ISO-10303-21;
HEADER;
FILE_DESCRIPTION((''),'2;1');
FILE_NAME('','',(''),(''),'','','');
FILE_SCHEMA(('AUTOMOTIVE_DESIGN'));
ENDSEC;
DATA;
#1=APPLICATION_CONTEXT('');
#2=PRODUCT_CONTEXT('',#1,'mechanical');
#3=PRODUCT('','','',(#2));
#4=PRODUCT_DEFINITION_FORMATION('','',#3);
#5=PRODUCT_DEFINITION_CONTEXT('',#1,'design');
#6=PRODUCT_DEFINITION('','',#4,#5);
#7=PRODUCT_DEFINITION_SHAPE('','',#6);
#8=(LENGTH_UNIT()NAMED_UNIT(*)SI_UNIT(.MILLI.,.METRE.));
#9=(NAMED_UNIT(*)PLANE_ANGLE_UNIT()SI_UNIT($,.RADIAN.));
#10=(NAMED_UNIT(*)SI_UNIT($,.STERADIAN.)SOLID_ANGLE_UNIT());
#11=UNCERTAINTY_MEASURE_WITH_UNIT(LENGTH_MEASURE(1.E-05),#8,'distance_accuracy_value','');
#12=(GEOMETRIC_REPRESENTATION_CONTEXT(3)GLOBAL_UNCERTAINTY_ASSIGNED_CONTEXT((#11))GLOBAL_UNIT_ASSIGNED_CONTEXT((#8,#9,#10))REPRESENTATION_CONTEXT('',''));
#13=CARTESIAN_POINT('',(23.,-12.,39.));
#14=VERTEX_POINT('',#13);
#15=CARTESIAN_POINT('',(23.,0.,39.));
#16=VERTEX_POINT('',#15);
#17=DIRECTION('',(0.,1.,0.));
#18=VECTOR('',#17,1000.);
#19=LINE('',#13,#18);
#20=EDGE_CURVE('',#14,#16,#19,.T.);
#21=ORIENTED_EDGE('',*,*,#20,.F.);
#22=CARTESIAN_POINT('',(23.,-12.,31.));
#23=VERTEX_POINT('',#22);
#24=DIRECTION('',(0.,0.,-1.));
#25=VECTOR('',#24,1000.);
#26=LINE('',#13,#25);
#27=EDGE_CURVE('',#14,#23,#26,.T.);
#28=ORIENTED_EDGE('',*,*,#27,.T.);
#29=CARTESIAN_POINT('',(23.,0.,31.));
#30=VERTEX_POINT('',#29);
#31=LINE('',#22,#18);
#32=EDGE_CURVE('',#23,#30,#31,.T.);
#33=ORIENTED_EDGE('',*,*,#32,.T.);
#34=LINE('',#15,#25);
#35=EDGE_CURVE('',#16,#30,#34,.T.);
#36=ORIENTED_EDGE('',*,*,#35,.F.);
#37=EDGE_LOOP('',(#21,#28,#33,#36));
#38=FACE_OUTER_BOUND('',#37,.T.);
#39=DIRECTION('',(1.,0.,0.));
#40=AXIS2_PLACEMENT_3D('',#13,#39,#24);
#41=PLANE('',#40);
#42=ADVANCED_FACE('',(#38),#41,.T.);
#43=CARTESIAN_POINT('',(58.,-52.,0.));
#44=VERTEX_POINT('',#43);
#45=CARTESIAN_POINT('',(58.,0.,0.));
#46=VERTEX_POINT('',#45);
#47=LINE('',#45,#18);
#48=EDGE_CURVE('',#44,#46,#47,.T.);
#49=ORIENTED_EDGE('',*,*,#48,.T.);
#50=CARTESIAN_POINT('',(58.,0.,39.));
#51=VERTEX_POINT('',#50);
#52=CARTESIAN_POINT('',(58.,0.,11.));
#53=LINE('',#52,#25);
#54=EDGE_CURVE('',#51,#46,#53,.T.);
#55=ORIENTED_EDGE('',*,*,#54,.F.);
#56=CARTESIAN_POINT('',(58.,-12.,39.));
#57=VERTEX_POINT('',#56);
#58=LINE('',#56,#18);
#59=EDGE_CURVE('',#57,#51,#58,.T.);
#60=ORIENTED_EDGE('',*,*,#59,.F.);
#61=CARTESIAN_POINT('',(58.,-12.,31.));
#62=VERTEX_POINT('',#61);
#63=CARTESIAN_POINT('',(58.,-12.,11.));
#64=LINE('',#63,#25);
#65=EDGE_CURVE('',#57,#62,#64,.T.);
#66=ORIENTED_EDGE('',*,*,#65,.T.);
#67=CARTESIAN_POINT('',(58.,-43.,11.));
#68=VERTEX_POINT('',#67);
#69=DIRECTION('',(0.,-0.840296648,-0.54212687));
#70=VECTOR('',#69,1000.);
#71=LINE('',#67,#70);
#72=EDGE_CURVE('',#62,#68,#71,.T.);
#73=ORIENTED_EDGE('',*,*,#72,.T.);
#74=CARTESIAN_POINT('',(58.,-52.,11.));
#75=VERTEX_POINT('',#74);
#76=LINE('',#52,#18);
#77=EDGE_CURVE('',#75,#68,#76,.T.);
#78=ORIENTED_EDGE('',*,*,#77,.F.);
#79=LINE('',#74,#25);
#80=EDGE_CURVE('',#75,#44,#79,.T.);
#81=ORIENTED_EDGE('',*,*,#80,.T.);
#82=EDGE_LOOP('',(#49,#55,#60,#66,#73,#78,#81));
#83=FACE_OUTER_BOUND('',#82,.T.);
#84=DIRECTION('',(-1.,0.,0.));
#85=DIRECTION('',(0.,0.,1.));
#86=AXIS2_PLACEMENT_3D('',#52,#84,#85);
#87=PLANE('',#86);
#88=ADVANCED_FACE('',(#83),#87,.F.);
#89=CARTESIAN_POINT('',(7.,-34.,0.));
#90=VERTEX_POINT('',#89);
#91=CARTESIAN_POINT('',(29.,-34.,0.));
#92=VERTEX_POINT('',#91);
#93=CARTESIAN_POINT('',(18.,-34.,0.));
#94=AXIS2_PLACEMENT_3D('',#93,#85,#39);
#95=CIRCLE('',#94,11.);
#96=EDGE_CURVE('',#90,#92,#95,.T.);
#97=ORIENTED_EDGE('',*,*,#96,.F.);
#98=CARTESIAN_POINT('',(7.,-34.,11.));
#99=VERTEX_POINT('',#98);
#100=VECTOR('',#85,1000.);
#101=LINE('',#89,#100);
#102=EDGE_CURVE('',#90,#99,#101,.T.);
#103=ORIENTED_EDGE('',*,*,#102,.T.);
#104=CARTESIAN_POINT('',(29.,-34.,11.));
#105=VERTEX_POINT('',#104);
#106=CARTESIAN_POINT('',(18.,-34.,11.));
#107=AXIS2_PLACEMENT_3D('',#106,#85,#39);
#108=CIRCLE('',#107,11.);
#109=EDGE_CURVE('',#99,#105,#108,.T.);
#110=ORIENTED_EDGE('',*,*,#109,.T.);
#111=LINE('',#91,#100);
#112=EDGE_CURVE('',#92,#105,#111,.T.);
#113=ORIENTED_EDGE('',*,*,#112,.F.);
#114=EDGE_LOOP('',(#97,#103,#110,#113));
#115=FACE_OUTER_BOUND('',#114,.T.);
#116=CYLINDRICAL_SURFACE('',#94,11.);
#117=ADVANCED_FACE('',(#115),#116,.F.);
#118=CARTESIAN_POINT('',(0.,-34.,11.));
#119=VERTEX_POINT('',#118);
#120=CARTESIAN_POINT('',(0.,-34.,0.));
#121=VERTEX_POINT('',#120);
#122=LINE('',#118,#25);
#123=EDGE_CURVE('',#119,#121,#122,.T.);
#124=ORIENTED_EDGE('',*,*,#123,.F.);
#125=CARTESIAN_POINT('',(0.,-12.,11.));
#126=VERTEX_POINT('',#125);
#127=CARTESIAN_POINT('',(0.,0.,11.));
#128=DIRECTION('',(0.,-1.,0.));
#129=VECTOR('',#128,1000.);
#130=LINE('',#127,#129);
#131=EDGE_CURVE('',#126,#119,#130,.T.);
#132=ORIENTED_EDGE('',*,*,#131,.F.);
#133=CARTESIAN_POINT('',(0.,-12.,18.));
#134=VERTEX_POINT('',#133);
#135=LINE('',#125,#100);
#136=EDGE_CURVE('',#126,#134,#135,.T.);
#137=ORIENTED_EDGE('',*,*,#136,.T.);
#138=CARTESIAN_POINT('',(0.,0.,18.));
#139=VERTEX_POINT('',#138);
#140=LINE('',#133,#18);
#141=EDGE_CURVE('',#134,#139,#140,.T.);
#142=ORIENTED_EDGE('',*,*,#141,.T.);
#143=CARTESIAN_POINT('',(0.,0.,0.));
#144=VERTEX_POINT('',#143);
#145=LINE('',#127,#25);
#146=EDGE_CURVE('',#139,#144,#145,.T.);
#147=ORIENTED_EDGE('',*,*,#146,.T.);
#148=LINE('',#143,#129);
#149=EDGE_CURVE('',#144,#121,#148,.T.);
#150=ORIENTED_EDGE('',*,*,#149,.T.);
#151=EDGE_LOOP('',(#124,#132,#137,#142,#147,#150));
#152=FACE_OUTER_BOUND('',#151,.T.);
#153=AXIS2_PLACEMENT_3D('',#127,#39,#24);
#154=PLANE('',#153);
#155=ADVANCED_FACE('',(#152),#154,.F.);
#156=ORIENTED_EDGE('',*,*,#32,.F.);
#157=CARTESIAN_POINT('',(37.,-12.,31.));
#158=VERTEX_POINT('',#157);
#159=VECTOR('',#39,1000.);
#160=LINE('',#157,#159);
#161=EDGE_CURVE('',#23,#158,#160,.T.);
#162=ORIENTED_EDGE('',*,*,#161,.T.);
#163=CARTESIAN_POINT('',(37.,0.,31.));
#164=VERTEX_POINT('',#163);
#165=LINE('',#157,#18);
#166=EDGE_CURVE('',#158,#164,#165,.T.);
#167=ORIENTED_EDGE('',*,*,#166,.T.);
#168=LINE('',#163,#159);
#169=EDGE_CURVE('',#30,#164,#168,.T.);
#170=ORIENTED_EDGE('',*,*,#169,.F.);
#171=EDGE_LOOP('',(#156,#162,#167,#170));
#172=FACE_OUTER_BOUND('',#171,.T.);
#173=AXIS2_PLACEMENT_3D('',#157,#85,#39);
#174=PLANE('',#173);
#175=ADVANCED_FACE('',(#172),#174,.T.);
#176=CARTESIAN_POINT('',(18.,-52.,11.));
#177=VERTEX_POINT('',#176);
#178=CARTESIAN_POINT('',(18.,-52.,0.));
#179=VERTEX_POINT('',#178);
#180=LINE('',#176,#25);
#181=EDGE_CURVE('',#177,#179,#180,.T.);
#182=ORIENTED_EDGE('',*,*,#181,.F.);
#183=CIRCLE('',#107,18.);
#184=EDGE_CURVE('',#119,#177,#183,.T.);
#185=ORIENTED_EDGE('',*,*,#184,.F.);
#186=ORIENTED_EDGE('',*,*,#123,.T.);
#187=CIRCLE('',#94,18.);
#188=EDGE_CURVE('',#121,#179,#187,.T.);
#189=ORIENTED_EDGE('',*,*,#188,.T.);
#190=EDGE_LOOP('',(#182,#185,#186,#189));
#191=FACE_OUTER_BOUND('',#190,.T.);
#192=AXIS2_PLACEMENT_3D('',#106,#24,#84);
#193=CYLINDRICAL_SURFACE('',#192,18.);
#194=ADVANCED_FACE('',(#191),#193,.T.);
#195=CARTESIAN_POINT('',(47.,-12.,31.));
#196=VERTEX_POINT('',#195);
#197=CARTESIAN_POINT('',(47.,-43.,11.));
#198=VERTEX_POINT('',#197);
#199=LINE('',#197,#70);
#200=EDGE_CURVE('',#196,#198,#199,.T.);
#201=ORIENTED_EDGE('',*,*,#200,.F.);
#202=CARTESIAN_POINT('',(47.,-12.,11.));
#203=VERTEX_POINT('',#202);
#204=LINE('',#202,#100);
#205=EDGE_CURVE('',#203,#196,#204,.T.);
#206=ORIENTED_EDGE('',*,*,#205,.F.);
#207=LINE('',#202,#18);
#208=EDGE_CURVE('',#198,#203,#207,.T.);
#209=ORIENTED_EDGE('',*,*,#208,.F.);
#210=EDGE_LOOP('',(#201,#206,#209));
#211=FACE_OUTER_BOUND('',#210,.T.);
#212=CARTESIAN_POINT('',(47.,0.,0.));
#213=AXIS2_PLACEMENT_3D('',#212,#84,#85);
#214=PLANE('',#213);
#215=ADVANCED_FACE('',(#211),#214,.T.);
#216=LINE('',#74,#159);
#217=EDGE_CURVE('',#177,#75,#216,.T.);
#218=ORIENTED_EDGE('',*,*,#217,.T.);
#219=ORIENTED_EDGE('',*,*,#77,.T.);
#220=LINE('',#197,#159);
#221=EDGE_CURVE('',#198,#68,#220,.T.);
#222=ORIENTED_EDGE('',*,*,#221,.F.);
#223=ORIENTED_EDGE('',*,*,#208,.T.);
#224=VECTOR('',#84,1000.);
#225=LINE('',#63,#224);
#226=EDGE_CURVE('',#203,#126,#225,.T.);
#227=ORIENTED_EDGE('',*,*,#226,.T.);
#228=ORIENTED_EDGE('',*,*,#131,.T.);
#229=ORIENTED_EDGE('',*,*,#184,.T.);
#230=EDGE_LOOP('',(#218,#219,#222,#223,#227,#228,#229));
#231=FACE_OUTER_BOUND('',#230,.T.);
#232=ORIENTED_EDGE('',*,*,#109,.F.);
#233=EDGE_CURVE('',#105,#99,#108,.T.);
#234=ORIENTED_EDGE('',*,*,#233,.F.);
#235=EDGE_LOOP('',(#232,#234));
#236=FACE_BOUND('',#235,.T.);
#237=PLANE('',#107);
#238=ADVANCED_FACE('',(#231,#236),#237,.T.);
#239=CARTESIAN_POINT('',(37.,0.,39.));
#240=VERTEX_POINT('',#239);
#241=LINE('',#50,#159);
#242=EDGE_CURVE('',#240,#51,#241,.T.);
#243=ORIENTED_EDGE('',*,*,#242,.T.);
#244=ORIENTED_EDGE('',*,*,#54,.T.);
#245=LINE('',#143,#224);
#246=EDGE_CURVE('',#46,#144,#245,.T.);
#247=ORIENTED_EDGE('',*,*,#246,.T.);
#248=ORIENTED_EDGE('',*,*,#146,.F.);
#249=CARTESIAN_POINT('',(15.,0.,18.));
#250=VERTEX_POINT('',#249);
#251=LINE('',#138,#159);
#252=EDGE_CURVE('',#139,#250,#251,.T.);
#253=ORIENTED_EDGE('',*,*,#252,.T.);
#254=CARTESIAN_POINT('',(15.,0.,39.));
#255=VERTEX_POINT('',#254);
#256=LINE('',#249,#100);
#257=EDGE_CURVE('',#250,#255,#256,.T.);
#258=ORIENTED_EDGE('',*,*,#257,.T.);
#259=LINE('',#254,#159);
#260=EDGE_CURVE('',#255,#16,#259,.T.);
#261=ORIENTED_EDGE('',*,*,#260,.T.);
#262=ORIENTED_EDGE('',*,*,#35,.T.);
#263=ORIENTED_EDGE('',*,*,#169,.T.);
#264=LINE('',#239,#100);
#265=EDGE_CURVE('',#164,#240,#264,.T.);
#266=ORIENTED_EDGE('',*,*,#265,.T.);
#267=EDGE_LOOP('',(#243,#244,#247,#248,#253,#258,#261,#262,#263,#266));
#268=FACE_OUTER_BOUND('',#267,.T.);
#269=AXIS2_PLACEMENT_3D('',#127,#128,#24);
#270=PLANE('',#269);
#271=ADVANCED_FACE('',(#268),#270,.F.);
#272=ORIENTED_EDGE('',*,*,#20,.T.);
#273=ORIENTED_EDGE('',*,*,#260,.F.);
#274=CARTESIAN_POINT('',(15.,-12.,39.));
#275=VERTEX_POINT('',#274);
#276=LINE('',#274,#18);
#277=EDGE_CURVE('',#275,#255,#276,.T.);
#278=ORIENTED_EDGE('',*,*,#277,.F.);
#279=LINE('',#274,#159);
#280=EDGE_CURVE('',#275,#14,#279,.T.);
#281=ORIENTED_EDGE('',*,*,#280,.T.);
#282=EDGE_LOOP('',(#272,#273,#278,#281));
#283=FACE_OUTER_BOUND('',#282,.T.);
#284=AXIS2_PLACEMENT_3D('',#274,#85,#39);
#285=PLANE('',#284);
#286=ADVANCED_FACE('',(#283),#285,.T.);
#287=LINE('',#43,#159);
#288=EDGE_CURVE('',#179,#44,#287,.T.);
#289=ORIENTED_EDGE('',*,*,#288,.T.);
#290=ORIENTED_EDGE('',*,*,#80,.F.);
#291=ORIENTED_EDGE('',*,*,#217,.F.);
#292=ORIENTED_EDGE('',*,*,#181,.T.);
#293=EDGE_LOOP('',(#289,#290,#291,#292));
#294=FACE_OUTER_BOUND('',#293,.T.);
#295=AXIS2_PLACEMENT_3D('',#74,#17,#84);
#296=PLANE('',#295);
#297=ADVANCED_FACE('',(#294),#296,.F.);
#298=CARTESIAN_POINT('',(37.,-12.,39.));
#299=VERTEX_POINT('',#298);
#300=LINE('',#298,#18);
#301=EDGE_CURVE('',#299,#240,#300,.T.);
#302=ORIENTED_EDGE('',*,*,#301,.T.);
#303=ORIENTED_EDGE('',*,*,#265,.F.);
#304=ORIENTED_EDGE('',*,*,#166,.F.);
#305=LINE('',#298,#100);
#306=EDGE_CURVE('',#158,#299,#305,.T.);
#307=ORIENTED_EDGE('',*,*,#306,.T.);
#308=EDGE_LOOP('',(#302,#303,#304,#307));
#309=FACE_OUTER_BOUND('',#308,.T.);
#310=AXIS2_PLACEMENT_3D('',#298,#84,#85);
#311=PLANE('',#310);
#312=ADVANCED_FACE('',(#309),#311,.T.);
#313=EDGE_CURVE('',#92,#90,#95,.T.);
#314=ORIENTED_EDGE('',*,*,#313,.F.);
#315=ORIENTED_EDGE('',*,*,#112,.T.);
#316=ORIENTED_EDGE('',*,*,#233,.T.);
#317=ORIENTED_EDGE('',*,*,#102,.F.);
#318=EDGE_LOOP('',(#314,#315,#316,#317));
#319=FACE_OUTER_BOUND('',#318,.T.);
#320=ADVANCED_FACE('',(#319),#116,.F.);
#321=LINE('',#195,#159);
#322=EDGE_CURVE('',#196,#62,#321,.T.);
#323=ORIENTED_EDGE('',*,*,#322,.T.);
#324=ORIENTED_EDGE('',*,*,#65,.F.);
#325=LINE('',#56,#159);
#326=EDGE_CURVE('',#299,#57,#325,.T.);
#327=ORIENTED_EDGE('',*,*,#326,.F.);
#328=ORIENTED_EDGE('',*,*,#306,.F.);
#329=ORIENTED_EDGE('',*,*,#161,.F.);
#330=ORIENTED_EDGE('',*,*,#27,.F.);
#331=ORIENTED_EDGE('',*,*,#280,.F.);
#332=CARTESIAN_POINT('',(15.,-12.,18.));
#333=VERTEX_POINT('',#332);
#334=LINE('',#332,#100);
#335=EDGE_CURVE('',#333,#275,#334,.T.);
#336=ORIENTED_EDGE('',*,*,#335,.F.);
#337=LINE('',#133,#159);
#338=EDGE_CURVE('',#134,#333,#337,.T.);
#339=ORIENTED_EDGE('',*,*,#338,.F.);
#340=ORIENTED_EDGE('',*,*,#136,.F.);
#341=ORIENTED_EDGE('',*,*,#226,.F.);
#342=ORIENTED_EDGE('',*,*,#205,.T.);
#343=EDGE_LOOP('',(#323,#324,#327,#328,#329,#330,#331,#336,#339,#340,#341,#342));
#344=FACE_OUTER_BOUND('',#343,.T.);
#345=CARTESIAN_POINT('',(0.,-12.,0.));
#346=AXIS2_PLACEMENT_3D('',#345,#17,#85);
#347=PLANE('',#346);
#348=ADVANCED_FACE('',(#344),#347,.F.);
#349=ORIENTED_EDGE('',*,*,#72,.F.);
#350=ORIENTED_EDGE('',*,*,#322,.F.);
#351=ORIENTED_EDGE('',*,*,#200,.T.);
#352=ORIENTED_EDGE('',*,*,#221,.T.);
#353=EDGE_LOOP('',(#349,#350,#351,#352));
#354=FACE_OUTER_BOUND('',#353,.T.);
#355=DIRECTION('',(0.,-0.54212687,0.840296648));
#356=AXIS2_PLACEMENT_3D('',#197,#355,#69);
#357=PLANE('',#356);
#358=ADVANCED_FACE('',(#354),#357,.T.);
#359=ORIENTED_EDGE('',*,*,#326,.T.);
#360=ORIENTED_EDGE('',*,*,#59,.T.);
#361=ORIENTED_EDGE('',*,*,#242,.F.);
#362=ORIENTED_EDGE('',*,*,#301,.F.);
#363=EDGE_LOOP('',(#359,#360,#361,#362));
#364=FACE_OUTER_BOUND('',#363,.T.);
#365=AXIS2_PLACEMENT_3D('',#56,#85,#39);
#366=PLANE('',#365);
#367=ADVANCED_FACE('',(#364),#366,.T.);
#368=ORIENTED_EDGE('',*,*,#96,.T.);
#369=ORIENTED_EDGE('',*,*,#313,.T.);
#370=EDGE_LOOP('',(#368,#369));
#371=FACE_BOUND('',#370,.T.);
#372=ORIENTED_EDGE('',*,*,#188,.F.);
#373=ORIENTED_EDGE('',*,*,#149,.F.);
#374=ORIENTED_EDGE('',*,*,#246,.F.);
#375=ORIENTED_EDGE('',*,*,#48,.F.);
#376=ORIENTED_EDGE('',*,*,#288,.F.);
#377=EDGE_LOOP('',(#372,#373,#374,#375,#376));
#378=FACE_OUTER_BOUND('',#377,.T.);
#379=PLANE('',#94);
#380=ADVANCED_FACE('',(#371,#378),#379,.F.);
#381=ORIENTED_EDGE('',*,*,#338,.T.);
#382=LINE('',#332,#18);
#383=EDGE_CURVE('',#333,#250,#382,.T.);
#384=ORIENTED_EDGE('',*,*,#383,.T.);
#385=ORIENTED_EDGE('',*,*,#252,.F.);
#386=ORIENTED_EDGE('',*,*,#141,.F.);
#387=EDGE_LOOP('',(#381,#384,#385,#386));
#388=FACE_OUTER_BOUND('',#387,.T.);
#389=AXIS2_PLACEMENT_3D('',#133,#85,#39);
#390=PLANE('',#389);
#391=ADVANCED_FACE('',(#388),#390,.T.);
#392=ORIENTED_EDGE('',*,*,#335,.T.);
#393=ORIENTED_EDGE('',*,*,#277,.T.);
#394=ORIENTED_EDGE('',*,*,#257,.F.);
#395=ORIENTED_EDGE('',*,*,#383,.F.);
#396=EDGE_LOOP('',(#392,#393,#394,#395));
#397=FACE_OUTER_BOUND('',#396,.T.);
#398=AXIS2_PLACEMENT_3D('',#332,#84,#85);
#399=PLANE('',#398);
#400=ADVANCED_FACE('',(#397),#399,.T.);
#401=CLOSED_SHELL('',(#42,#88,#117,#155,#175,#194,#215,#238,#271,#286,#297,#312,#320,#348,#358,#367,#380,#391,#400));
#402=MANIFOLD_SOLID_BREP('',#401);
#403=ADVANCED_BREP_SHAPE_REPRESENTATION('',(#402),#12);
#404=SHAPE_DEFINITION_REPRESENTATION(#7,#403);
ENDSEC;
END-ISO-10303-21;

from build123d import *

# Parameters (mm, degrees)
BASE_BLOCK_DEPTH = 11
TOP_PLATE_DEPTH  = 12
GUSSET_RIB_DEPTH = 11
CUT_22_PROFILE_R = 11
CUT_22_DEPTH     = 11


with BuildPart() as part:
    # Base Block Profile → Base Block (new body)
    with BuildSketch(Plane.XY):
        with BuildLine():
            Line((58, 0), (58, -52))
            Line((58, -52), (18, -52))
            ThreePointArc((18, -52), (5.272077939, -46.727922061), (0, -34))
            Line((0, -34), (0, 0))
            Line((0, 0), (58, 0))
        make_face()
    extrude(amount=BASE_BLOCK_DEPTH)

    # Top Plate Profile → Top Plate (add)
    with BuildSketch(Plane(origin=(0, 0, 0), x_dir=(1, 0, 0), z_dir=(0, 1, 0))):
        Polygon((58, -11), (58, -39), (37, -39), (37, -31), (23, -31), (23, -39), (15, -39), (15, -18), (0, -18), (0, -11), align=None)
    extrude(amount=-TOP_PLATE_DEPTH)

    # Gusset Profile → Gusset Rib (add)
    with BuildSketch(Plane(origin=(58, 0, 0), x_dir=(0, 0, -1), z_dir=(1, 0, 0))):
        Polygon((-11, -12), (-31, -12), (-11, -43), align=None)
    extrude(amount=-GUSSET_RIB_DEPTH)

    # Cut Ø22 Profile → Cut Ø22 (cut)
    with BuildSketch(Plane.XY.offset(11)):
        with Locations((18, -34)):
            Circle(CUT_22_PROFILE_R)
    extrude(amount=-CUT_22_DEPTH, mode=Mode.SUBTRACT)


solid = part.part
